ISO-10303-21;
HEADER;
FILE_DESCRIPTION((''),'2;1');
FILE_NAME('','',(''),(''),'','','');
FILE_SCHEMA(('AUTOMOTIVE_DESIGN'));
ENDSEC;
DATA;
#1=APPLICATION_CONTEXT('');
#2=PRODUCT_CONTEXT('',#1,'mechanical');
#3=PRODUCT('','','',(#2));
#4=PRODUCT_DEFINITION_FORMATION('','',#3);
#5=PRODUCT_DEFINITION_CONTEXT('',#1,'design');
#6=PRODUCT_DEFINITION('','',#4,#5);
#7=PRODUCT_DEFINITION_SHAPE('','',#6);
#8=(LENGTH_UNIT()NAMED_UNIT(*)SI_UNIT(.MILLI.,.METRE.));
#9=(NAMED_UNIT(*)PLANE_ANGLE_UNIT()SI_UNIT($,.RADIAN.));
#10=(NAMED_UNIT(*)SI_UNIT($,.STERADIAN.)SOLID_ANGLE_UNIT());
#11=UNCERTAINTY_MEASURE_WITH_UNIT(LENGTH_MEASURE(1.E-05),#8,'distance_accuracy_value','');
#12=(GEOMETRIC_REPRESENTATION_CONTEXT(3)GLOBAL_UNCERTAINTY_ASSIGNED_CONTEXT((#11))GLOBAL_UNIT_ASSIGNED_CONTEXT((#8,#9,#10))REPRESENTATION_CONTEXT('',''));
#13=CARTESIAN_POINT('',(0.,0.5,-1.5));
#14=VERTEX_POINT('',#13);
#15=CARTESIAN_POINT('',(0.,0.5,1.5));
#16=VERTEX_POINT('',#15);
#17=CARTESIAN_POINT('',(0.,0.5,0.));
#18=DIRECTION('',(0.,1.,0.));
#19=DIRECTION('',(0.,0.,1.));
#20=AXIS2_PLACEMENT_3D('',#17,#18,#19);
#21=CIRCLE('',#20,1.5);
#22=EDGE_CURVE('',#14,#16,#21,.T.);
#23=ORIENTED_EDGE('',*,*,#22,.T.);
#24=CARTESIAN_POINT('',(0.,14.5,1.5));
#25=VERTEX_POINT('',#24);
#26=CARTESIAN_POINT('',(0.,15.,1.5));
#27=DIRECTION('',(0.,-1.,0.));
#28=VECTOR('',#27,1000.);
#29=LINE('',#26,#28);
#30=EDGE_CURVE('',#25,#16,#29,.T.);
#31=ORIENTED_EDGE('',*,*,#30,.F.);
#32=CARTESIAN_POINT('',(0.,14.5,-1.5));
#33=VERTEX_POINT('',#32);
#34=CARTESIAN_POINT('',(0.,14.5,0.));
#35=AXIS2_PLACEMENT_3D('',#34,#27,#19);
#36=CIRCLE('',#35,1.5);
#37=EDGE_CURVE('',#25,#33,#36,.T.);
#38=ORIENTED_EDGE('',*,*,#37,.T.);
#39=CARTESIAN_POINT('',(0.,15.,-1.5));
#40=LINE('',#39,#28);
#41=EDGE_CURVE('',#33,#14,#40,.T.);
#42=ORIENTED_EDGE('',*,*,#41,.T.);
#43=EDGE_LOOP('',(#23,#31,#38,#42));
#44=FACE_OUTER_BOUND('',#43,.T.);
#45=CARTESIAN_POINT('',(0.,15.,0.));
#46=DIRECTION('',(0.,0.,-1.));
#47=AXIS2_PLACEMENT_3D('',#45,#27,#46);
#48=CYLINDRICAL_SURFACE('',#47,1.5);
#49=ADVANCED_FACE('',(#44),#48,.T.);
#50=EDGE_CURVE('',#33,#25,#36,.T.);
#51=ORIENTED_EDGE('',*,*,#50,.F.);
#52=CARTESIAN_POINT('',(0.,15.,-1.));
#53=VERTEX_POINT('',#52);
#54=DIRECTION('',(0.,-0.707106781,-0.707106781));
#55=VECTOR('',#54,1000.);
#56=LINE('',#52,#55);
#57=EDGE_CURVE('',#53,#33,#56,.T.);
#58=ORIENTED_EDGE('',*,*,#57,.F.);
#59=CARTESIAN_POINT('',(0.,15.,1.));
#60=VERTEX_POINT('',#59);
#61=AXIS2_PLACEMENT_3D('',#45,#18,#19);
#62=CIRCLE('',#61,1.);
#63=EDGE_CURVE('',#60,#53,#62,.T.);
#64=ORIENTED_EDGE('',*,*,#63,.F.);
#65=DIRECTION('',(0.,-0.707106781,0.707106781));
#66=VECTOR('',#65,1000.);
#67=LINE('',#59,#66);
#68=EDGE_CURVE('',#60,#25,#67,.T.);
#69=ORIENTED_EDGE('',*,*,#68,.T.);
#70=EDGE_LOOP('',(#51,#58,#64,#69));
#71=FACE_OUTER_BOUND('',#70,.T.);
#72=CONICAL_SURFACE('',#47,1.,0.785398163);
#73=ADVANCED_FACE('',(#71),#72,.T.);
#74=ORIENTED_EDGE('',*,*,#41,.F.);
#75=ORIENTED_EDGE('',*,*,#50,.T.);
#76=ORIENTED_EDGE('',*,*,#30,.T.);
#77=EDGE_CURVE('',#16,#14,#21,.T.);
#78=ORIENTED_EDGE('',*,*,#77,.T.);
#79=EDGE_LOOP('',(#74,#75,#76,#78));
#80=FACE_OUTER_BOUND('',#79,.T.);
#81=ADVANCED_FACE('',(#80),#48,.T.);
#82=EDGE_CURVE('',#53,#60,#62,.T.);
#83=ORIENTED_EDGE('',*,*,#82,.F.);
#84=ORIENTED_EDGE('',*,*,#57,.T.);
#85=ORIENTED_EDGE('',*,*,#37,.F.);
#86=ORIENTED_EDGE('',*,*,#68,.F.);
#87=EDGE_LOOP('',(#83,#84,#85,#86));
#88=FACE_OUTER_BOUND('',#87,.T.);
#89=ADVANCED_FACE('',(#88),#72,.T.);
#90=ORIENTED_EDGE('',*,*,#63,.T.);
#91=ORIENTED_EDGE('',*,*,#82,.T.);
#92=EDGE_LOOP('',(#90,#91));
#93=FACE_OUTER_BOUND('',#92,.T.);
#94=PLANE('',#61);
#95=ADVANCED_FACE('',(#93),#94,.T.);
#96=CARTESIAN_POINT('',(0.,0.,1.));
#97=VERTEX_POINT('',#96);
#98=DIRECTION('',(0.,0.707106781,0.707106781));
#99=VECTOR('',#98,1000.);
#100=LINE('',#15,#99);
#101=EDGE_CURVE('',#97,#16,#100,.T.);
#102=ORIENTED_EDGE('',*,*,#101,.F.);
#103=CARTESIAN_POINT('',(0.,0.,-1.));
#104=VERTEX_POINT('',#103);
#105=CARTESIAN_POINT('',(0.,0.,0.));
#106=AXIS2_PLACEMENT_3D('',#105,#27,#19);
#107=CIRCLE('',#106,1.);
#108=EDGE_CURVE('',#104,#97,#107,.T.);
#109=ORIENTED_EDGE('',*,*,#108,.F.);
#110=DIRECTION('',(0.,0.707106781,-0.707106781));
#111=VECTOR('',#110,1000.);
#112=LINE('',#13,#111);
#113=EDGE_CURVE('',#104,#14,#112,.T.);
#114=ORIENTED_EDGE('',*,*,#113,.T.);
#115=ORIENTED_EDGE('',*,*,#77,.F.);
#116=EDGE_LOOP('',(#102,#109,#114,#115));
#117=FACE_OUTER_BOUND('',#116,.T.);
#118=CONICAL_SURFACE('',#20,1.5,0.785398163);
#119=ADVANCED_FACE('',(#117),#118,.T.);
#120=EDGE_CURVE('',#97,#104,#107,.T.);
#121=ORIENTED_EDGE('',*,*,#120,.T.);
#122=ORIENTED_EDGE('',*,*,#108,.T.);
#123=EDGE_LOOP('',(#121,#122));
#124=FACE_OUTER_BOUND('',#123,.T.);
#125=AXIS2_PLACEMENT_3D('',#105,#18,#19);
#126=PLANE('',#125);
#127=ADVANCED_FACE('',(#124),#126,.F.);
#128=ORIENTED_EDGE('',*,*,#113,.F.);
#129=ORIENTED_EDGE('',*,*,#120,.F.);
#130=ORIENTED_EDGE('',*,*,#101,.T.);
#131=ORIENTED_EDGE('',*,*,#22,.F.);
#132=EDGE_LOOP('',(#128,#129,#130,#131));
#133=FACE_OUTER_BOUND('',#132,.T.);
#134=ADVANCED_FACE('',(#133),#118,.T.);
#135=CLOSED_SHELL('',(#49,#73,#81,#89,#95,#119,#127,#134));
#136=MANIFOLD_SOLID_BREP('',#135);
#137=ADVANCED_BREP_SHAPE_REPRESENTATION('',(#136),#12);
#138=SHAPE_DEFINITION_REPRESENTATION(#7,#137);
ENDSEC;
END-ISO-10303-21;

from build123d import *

# Parameters (mm, degrees)
SKETCH1_R           = 1.5
BOSS_EXTRUDE1_DEPTH = 15
CHAMFER1_SIZE       = 0.5


with BuildPart() as part:
    # Sketch1 → Boss-Extrude1 (new body)
    with BuildSketch(Plane(origin=(0, 0, 0), x_dir=(1, 0, 0), z_dir=(0, 1, 0))):
        with Locations(Location((0, 0, 0), (0, 0, 270))):
            Circle(SKETCH1_R)
    extrude(amount=BOSS_EXTRUDE1_DEPTH)

    # Chamfer1
    chamfer1_edges = [part.edges().sort_by_distance(p)[0] for p in [
        (0, 0, -1.5),
        (0, 15, -1.5),
    ]]
    chamfer(chamfer1_edges, length=CHAMFER1_SIZE)


solid = part.part
